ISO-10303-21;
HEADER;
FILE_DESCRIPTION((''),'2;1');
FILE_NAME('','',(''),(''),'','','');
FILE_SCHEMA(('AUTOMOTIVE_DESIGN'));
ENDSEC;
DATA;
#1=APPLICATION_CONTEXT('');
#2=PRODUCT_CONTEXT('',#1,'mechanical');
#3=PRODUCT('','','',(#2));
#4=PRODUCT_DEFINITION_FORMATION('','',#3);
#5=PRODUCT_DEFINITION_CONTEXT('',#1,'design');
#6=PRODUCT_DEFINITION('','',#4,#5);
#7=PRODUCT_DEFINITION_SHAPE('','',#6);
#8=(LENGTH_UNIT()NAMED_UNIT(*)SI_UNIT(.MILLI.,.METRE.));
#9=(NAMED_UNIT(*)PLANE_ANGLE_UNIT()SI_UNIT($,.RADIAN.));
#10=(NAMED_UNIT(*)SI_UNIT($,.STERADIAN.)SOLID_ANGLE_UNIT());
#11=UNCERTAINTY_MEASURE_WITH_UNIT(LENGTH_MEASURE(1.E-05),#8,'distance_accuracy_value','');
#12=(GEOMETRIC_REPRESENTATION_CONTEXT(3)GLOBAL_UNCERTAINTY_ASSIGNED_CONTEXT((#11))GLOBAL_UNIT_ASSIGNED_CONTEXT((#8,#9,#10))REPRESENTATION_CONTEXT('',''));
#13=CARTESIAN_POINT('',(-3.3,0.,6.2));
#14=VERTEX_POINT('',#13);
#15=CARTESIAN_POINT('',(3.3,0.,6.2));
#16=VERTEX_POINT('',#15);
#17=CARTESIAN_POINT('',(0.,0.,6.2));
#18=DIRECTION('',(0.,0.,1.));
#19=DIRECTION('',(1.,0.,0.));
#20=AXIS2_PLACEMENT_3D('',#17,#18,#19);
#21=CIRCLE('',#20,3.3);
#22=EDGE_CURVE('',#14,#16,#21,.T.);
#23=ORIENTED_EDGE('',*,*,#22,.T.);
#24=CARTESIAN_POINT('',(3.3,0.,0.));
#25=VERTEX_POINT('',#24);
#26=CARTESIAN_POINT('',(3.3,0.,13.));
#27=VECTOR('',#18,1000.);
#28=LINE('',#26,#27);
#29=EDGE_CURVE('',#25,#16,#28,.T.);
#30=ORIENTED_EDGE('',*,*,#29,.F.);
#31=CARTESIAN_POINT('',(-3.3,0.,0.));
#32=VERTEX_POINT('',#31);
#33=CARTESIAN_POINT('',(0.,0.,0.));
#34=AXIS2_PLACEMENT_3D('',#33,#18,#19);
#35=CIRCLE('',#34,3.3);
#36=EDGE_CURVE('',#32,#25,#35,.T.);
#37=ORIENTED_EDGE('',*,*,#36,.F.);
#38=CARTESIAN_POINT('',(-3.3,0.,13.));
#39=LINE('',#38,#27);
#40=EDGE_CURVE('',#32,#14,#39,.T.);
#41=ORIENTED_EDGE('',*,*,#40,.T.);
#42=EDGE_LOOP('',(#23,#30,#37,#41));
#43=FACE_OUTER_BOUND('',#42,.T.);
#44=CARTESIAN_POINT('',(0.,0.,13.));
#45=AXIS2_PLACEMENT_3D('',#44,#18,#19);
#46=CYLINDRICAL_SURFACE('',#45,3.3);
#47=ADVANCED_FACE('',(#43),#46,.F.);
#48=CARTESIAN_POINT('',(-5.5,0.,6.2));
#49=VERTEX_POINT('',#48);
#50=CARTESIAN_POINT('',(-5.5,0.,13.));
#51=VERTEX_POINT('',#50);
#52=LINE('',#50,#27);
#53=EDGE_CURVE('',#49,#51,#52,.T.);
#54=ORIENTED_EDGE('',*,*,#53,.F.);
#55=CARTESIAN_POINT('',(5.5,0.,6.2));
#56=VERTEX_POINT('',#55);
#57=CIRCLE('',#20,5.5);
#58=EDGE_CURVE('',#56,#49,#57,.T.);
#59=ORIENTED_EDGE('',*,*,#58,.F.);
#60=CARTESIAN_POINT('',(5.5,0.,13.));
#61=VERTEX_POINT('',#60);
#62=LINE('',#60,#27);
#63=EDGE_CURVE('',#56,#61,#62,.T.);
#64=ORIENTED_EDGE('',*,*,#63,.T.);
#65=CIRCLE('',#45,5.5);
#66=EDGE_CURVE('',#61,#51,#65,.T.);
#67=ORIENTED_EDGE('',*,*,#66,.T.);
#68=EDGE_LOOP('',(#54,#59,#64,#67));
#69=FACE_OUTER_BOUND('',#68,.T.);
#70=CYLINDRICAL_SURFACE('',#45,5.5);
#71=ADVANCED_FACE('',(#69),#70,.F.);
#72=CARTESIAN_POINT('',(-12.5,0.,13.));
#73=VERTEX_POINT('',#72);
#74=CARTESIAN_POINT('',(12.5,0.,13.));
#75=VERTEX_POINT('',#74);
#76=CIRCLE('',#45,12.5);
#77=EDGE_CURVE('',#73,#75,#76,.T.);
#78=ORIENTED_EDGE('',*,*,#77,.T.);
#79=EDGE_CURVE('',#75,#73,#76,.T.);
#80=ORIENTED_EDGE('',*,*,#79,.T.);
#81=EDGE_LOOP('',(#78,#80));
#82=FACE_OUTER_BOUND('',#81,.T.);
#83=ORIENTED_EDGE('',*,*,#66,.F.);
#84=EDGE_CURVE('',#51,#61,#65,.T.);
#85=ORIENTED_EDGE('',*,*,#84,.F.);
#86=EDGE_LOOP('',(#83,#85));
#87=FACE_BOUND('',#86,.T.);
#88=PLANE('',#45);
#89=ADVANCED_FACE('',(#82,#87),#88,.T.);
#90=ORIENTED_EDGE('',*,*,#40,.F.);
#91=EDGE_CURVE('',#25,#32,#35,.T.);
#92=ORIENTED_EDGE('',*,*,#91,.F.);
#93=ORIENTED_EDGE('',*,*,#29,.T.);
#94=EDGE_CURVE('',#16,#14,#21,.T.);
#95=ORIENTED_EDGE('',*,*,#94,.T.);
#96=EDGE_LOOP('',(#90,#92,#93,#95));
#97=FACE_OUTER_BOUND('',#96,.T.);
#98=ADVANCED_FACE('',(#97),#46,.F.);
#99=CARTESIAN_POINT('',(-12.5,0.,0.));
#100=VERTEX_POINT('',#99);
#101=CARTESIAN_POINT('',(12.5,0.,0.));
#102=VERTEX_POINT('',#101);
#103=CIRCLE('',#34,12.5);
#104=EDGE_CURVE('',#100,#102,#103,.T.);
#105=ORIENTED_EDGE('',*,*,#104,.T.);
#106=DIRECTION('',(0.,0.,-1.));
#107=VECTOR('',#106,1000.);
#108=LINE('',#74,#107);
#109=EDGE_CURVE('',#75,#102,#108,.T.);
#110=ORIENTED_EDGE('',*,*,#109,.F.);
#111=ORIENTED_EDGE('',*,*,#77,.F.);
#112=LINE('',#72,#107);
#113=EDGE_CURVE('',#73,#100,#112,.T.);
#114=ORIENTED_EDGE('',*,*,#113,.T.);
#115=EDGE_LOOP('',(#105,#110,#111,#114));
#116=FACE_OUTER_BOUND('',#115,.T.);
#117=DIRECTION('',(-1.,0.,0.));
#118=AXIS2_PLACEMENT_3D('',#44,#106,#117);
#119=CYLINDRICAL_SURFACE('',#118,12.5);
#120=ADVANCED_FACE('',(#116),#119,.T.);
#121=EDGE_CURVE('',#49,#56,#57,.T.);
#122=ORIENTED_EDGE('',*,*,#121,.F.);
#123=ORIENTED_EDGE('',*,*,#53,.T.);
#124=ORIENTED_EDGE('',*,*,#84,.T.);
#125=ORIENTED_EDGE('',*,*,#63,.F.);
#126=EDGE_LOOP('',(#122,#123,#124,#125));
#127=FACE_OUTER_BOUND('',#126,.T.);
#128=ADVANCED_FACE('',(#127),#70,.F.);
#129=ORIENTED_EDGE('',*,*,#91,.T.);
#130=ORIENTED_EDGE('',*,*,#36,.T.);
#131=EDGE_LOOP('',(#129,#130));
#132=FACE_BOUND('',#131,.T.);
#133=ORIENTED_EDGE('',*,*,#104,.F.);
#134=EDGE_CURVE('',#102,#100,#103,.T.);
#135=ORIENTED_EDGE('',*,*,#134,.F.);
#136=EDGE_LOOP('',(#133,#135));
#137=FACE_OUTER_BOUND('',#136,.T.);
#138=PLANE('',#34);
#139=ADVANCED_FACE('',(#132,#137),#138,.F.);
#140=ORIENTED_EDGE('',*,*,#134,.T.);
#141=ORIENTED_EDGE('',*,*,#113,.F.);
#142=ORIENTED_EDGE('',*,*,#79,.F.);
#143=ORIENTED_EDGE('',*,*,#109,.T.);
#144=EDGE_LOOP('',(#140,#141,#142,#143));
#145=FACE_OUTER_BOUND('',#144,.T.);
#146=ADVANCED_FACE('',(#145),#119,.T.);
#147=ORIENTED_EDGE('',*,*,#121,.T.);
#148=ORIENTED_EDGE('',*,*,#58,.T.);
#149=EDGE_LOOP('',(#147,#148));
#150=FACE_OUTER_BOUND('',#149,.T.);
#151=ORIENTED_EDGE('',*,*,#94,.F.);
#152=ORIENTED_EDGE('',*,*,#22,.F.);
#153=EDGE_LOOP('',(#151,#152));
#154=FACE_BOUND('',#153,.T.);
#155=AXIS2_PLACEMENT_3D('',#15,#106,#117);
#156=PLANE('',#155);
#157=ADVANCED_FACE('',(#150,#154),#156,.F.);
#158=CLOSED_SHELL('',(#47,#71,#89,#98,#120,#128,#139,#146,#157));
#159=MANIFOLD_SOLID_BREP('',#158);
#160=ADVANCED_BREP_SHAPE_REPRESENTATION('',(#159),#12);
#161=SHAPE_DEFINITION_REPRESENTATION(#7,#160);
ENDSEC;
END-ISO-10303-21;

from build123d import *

# Parameters (mm, degrees)
SKETCH_1_R                   = 12.5
EXTRUDE_1_DEPTH              = 13
HOLE_WIZARD_M6_1_D           = 6.6
HOLE_WIZARD_M6_1_CBORE_D     = 11
HOLE_WIZARD_M6_1_CBORE_DEPTH = 6.8


with BuildPart() as part:
    # 草图1 → 凸台-拉伸1 (new body)
    with BuildSketch(Plane.XY):
        with Locations(Location((0, 0, 0), (0, 0, 180))):
            Circle(SKETCH_1_R)
    extrude(amount=EXTRUDE_1_DEPTH)

    # M6 六角圆柱头螺钉的柱形沉头孔1 (through all)
    with Locations(Plane.XY.offset(13)):
        with Locations((0, 0)):
            CounterBoreHole(HOLE_WIZARD_M6_1_D / 2, HOLE_WIZARD_M6_1_CBORE_D / 2, HOLE_WIZARD_M6_1_CBORE_DEPTH)


solid = part.part
